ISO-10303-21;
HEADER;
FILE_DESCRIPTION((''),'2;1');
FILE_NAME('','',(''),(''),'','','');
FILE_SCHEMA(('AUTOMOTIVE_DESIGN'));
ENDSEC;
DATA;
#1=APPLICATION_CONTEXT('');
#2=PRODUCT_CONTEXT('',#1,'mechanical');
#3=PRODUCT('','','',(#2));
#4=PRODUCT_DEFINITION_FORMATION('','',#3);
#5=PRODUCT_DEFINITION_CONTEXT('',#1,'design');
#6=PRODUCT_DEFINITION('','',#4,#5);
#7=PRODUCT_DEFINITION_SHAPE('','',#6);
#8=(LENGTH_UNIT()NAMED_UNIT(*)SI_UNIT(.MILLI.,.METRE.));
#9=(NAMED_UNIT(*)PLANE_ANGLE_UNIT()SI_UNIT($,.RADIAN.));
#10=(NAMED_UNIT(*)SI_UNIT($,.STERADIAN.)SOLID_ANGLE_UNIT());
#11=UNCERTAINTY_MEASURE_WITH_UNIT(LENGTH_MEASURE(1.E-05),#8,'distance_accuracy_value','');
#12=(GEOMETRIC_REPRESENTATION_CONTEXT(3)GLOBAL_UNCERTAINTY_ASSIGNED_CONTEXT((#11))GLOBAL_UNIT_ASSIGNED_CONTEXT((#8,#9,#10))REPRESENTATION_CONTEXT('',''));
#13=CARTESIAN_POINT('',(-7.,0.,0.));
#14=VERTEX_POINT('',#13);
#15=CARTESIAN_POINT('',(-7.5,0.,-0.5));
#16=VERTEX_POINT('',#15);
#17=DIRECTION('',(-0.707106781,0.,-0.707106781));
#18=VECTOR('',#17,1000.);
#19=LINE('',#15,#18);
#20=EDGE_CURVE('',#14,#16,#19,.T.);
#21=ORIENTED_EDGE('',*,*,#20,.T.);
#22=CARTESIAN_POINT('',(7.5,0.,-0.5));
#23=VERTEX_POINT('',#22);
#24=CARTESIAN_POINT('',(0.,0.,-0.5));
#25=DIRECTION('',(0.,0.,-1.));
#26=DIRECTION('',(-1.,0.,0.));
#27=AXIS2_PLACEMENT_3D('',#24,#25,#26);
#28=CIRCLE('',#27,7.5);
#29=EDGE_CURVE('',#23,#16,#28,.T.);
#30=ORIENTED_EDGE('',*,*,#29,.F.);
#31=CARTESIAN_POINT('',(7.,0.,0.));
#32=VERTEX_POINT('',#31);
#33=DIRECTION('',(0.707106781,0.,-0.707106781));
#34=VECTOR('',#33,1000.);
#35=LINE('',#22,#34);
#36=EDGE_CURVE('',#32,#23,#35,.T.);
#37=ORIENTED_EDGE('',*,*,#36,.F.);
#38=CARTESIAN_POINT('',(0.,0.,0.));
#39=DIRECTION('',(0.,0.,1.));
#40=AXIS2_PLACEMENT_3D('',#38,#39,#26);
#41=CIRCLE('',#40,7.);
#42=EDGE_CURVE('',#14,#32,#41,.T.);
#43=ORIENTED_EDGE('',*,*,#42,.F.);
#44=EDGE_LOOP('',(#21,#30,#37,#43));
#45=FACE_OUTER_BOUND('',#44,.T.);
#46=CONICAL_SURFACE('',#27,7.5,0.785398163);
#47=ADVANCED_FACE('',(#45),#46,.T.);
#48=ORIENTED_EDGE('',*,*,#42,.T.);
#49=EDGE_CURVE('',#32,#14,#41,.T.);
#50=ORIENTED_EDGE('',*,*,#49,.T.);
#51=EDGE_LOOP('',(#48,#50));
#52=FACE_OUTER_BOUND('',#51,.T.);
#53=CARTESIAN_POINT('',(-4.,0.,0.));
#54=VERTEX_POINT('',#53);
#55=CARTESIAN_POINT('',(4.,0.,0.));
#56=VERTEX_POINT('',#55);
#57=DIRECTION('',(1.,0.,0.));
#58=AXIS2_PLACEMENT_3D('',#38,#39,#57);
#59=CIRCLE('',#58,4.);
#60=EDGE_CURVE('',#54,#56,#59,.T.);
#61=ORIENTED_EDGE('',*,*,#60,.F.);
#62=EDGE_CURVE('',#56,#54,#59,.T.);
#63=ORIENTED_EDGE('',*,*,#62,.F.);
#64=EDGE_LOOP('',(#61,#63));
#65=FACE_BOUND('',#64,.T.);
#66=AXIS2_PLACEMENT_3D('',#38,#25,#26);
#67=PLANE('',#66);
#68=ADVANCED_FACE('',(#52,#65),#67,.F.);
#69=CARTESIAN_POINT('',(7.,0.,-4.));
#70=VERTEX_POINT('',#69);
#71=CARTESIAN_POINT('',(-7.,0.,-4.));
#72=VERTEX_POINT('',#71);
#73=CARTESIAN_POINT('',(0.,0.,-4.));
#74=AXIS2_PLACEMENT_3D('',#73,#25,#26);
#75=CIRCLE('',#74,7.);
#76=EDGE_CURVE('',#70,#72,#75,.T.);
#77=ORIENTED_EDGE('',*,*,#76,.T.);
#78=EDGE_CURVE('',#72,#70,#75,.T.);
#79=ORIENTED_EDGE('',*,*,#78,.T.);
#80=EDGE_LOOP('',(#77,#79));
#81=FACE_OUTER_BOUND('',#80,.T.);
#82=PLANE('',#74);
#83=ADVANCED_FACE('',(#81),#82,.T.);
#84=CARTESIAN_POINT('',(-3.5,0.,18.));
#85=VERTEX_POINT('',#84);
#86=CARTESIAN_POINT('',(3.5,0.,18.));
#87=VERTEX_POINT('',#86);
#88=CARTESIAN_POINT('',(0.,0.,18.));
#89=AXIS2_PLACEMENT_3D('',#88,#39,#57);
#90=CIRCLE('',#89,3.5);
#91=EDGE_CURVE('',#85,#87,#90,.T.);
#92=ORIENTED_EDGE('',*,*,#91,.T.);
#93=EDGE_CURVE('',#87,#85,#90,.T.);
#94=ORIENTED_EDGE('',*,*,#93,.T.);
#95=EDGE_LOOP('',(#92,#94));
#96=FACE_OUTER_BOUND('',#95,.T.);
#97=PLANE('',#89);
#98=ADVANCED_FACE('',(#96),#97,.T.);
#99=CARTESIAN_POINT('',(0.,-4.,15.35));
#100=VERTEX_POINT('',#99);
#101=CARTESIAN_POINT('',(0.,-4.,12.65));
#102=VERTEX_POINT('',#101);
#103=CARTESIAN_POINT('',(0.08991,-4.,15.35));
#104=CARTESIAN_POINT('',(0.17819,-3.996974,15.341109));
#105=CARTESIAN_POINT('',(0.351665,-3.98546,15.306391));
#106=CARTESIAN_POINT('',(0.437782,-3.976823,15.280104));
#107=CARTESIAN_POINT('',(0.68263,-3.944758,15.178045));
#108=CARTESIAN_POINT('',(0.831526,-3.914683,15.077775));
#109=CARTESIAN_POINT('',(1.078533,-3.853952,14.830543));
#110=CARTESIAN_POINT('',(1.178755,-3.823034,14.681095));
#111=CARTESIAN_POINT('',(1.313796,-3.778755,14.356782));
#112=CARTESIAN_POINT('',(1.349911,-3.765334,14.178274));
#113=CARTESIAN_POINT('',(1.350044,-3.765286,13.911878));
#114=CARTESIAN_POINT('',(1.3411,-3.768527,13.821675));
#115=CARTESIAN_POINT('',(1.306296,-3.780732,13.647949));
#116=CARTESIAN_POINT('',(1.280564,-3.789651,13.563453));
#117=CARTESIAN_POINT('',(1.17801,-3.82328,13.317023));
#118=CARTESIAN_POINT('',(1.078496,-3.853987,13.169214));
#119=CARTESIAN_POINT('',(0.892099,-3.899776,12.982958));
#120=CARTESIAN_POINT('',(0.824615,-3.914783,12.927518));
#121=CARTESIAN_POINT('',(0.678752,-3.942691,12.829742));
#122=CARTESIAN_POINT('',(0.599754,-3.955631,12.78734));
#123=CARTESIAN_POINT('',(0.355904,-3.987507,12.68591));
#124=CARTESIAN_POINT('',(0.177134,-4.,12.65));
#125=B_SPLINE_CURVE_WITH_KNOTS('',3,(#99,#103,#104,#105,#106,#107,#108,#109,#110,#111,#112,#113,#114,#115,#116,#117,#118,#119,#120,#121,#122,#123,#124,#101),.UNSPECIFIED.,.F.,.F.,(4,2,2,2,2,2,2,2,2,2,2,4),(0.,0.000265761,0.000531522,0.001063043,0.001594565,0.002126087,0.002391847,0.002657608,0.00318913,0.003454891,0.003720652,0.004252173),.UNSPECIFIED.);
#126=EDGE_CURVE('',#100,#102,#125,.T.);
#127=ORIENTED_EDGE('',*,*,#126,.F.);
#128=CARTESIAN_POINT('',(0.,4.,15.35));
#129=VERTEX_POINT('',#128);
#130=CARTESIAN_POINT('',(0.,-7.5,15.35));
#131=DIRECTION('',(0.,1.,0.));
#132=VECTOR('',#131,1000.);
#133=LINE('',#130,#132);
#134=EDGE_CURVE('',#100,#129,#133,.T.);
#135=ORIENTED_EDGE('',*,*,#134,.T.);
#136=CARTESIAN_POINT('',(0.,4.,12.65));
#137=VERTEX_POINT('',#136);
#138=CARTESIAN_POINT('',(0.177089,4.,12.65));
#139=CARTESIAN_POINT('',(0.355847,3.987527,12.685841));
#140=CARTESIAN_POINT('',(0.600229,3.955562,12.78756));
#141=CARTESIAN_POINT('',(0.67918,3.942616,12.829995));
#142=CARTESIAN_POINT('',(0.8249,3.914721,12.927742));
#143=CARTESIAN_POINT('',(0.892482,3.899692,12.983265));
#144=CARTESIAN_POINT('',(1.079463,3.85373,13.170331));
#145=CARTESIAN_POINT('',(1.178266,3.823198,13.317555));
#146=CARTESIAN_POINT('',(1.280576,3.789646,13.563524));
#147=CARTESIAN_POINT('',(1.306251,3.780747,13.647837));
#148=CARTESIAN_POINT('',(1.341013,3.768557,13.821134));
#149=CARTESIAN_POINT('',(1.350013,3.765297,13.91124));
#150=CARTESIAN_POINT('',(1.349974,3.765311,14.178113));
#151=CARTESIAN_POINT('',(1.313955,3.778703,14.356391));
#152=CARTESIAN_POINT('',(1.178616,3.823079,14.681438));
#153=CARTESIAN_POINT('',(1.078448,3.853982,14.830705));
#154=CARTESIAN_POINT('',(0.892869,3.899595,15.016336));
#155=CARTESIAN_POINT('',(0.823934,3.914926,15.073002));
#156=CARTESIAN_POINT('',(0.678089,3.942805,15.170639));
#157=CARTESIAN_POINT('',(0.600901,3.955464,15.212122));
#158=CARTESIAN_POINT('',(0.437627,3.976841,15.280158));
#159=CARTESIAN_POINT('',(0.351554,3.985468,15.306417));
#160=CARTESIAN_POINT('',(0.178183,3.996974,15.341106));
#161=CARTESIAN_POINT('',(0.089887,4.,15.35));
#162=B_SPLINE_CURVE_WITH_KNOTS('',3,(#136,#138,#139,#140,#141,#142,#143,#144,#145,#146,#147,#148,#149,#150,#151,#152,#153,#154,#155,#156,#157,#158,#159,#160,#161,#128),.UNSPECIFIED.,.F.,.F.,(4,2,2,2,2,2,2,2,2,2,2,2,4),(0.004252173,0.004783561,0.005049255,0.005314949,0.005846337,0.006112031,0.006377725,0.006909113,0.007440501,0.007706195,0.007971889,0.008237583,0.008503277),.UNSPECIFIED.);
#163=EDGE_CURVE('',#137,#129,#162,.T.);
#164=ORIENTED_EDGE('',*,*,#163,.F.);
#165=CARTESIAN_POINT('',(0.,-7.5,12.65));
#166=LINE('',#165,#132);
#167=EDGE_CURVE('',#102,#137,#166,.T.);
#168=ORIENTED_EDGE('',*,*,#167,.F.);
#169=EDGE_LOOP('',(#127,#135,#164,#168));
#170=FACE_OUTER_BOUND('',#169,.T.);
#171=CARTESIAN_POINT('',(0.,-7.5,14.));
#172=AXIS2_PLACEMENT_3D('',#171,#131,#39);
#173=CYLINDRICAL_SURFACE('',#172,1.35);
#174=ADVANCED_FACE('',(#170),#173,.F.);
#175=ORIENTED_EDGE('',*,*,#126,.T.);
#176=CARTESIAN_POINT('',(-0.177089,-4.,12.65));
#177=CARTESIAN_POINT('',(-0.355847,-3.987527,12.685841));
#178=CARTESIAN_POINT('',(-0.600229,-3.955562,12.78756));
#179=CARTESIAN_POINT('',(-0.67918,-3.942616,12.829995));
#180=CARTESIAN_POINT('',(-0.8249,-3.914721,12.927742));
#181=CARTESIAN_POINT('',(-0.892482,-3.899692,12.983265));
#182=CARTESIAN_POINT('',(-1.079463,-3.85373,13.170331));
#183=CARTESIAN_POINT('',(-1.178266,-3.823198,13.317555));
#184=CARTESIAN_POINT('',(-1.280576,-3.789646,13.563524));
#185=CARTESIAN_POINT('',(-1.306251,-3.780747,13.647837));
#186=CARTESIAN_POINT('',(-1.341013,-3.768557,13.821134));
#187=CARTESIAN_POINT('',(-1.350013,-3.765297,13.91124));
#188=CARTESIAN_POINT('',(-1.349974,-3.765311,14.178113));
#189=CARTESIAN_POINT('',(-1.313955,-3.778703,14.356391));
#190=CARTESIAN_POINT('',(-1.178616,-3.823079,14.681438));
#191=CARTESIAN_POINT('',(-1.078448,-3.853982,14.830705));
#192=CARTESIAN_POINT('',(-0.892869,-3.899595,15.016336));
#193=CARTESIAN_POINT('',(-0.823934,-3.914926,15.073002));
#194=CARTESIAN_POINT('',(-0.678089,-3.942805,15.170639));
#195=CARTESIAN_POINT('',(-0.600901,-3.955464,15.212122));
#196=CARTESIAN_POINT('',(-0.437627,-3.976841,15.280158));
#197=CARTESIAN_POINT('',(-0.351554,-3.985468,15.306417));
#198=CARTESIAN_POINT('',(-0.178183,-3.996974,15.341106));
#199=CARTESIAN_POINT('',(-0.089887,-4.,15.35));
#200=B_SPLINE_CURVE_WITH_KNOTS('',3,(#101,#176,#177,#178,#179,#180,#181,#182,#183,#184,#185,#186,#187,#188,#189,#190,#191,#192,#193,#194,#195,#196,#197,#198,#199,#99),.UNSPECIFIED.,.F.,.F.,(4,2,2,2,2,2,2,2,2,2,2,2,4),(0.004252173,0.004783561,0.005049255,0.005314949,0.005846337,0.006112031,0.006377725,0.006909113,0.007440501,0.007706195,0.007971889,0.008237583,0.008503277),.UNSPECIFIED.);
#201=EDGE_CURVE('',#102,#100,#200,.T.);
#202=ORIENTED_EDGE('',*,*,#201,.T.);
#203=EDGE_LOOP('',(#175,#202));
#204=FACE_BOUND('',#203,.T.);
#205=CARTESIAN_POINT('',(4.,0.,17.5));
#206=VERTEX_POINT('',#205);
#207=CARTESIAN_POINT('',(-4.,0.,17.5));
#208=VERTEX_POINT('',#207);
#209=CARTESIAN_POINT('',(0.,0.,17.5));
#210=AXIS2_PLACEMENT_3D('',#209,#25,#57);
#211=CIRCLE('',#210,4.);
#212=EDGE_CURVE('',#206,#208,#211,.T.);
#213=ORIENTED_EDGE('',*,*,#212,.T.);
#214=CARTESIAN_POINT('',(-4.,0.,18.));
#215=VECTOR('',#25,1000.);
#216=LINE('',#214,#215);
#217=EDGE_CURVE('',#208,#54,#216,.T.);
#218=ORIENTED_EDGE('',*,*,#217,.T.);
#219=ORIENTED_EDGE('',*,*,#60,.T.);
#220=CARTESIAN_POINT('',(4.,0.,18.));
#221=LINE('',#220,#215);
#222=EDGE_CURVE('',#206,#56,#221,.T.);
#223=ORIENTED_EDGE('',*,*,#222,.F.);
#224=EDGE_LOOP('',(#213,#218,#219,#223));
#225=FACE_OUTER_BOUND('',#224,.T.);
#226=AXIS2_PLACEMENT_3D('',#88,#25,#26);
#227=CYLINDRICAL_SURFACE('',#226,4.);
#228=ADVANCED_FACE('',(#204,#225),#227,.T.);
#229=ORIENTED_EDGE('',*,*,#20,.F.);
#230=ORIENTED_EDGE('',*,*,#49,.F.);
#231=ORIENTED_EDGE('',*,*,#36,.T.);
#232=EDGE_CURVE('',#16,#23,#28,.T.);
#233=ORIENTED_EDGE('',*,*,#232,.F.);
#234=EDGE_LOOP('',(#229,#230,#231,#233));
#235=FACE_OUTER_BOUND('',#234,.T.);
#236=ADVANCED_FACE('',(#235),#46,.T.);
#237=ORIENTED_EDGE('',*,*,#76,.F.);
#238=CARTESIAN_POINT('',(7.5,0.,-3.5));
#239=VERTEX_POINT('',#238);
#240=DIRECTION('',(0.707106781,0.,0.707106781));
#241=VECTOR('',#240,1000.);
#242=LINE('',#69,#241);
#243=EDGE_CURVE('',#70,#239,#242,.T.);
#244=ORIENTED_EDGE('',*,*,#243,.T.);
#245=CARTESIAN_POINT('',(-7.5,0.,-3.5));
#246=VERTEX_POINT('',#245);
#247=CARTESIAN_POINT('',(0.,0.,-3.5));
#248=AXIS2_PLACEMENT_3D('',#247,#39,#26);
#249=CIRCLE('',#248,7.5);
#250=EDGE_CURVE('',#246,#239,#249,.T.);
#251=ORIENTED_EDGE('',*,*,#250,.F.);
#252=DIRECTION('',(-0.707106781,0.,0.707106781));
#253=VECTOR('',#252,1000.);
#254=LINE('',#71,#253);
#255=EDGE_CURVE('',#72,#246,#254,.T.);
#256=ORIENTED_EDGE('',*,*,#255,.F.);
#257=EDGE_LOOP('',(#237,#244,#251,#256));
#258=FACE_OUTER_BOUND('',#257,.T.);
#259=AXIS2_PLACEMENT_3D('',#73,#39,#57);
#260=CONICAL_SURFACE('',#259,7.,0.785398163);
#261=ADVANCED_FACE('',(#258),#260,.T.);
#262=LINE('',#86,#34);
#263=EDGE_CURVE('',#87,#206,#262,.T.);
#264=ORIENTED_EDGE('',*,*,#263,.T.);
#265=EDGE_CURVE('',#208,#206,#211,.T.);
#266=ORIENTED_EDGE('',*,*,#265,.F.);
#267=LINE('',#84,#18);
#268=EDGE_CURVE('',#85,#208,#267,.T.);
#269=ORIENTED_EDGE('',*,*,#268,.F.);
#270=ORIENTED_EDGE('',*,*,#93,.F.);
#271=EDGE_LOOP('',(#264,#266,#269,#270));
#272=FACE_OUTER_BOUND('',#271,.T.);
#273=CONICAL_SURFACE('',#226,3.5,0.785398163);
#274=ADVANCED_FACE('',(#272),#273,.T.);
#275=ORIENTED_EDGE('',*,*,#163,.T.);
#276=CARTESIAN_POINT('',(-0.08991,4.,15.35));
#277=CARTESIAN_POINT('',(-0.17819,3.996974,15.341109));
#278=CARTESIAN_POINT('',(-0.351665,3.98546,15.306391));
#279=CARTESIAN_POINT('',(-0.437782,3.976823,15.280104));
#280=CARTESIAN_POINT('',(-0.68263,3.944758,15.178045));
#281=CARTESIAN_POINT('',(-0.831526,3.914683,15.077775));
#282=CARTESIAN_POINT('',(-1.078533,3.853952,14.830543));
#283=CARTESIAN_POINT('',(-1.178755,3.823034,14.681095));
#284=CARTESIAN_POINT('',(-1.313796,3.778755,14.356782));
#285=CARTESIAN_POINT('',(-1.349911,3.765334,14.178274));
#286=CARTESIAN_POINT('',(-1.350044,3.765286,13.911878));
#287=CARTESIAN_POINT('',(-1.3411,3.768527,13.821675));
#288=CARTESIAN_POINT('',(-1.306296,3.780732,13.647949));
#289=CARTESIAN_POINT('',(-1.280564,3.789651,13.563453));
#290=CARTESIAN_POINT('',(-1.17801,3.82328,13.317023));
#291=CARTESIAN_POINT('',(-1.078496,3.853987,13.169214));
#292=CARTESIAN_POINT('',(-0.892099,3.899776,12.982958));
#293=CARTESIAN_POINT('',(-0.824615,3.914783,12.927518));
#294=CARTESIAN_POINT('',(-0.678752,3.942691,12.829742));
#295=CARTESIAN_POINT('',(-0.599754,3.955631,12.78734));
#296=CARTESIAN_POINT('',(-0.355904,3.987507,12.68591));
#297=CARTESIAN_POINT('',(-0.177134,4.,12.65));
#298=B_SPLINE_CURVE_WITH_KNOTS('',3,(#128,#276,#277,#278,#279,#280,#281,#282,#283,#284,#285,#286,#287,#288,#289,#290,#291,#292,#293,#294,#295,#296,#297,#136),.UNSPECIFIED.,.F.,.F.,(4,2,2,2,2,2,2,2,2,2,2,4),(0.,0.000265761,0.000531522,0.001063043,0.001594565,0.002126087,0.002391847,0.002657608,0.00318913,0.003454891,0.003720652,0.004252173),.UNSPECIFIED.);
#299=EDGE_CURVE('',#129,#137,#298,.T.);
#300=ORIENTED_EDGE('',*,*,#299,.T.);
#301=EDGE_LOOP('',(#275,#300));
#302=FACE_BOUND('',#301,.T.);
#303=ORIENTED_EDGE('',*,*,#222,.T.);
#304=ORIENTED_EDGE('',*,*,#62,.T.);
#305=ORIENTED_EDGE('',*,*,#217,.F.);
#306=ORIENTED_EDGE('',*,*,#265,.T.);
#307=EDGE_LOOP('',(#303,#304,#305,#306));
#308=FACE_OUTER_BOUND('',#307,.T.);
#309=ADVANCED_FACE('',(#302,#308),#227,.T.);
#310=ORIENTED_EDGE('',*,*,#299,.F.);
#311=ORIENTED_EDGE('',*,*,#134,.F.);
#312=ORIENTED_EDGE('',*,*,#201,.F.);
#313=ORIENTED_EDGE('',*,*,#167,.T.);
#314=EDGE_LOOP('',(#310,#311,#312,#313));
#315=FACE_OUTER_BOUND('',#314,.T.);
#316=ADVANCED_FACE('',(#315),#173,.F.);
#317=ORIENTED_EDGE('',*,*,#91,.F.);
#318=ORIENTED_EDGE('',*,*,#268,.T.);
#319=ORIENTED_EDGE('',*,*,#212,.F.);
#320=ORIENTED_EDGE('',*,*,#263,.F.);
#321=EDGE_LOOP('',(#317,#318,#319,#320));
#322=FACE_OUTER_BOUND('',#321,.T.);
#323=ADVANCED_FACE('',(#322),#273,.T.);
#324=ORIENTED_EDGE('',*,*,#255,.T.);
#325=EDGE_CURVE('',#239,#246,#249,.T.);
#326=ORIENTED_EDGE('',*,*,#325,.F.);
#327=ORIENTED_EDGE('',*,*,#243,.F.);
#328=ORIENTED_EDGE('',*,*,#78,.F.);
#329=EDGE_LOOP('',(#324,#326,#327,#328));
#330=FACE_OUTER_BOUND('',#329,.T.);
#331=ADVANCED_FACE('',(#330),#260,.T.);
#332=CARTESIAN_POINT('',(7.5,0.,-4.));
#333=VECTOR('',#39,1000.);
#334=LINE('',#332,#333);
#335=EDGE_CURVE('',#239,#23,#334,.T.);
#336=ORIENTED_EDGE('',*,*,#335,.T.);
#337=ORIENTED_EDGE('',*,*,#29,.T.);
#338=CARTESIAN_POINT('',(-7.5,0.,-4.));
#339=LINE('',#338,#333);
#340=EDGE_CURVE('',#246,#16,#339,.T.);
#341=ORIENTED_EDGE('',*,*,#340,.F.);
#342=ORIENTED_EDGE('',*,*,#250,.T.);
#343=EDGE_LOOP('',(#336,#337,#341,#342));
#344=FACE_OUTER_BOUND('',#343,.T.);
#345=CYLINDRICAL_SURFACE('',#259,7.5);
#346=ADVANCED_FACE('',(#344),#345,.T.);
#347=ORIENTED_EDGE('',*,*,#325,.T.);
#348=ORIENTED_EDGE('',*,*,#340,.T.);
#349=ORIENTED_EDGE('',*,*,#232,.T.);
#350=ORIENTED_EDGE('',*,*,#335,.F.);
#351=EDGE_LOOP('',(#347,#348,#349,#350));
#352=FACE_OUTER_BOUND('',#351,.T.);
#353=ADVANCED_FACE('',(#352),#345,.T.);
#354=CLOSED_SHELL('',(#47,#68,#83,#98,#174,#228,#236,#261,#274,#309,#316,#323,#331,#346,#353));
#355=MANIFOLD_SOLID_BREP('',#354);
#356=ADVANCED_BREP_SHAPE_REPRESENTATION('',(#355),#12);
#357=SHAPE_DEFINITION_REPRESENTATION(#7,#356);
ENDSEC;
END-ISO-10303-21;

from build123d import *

# Parameters (mm, degrees)
SKETCH1_R               = 4
BOSS_EXTRUDE1_DEPTH     = 18
SKETCH2_R               = 7.5
BOSS_EXTRUDE2_DEPTH     = 4
CUT_EXTRUDE1_DEPTH      = 21.892582416
CUT_EXTRUDE1_DEPTH_BACK = 21.892582416
SKETCH3_R               = 1.35
CHAMFER1_SIZE           = 0.5


with BuildPart() as part:
    # Sketch1 → Boss-Extrude1 (new body)
    with BuildSketch(Plane.XY):
        Circle(SKETCH1_R)
    extrude(amount=BOSS_EXTRUDE1_DEPTH)

    # Sketch2 → Boss-Extrude2 (add)
    with BuildSketch(Plane(origin=(0, 0, 0), x_dir=(-1, 0, 0), z_dir=(0, 0, -1))):
        Circle(SKETCH2_R)
    extrude(amount=BOSS_EXTRUDE2_DEPTH)

    # Sketch3 → Cut-Extrude1 (cut, two sides: drawn at the far end of the back side and taken through both)
    with BuildSketch(Plane(origin=(0, 0, 0), x_dir=(1, 0, 0), z_dir=(0, 1, 0)).offset(-CUT_EXTRUDE1_DEPTH_BACK)):
        with Locations(Location((0, -14, 0), (0, 0, 270))):
            Circle(SKETCH3_R)
    extrude(amount=CUT_EXTRUDE1_DEPTH + CUT_EXTRUDE1_DEPTH_BACK, mode=Mode.SUBTRACT)

    # Chamfer1
    chamfer1_edges = [part.edges().sort_by_distance(p)[0] for p in [
        (-4, 0, 18),
        (7.5, 0, 0),
        (7.5, 0, -4),
    ]]
    chamfer(chamfer1_edges, length=CHAMFER1_SIZE)


solid = part.part
